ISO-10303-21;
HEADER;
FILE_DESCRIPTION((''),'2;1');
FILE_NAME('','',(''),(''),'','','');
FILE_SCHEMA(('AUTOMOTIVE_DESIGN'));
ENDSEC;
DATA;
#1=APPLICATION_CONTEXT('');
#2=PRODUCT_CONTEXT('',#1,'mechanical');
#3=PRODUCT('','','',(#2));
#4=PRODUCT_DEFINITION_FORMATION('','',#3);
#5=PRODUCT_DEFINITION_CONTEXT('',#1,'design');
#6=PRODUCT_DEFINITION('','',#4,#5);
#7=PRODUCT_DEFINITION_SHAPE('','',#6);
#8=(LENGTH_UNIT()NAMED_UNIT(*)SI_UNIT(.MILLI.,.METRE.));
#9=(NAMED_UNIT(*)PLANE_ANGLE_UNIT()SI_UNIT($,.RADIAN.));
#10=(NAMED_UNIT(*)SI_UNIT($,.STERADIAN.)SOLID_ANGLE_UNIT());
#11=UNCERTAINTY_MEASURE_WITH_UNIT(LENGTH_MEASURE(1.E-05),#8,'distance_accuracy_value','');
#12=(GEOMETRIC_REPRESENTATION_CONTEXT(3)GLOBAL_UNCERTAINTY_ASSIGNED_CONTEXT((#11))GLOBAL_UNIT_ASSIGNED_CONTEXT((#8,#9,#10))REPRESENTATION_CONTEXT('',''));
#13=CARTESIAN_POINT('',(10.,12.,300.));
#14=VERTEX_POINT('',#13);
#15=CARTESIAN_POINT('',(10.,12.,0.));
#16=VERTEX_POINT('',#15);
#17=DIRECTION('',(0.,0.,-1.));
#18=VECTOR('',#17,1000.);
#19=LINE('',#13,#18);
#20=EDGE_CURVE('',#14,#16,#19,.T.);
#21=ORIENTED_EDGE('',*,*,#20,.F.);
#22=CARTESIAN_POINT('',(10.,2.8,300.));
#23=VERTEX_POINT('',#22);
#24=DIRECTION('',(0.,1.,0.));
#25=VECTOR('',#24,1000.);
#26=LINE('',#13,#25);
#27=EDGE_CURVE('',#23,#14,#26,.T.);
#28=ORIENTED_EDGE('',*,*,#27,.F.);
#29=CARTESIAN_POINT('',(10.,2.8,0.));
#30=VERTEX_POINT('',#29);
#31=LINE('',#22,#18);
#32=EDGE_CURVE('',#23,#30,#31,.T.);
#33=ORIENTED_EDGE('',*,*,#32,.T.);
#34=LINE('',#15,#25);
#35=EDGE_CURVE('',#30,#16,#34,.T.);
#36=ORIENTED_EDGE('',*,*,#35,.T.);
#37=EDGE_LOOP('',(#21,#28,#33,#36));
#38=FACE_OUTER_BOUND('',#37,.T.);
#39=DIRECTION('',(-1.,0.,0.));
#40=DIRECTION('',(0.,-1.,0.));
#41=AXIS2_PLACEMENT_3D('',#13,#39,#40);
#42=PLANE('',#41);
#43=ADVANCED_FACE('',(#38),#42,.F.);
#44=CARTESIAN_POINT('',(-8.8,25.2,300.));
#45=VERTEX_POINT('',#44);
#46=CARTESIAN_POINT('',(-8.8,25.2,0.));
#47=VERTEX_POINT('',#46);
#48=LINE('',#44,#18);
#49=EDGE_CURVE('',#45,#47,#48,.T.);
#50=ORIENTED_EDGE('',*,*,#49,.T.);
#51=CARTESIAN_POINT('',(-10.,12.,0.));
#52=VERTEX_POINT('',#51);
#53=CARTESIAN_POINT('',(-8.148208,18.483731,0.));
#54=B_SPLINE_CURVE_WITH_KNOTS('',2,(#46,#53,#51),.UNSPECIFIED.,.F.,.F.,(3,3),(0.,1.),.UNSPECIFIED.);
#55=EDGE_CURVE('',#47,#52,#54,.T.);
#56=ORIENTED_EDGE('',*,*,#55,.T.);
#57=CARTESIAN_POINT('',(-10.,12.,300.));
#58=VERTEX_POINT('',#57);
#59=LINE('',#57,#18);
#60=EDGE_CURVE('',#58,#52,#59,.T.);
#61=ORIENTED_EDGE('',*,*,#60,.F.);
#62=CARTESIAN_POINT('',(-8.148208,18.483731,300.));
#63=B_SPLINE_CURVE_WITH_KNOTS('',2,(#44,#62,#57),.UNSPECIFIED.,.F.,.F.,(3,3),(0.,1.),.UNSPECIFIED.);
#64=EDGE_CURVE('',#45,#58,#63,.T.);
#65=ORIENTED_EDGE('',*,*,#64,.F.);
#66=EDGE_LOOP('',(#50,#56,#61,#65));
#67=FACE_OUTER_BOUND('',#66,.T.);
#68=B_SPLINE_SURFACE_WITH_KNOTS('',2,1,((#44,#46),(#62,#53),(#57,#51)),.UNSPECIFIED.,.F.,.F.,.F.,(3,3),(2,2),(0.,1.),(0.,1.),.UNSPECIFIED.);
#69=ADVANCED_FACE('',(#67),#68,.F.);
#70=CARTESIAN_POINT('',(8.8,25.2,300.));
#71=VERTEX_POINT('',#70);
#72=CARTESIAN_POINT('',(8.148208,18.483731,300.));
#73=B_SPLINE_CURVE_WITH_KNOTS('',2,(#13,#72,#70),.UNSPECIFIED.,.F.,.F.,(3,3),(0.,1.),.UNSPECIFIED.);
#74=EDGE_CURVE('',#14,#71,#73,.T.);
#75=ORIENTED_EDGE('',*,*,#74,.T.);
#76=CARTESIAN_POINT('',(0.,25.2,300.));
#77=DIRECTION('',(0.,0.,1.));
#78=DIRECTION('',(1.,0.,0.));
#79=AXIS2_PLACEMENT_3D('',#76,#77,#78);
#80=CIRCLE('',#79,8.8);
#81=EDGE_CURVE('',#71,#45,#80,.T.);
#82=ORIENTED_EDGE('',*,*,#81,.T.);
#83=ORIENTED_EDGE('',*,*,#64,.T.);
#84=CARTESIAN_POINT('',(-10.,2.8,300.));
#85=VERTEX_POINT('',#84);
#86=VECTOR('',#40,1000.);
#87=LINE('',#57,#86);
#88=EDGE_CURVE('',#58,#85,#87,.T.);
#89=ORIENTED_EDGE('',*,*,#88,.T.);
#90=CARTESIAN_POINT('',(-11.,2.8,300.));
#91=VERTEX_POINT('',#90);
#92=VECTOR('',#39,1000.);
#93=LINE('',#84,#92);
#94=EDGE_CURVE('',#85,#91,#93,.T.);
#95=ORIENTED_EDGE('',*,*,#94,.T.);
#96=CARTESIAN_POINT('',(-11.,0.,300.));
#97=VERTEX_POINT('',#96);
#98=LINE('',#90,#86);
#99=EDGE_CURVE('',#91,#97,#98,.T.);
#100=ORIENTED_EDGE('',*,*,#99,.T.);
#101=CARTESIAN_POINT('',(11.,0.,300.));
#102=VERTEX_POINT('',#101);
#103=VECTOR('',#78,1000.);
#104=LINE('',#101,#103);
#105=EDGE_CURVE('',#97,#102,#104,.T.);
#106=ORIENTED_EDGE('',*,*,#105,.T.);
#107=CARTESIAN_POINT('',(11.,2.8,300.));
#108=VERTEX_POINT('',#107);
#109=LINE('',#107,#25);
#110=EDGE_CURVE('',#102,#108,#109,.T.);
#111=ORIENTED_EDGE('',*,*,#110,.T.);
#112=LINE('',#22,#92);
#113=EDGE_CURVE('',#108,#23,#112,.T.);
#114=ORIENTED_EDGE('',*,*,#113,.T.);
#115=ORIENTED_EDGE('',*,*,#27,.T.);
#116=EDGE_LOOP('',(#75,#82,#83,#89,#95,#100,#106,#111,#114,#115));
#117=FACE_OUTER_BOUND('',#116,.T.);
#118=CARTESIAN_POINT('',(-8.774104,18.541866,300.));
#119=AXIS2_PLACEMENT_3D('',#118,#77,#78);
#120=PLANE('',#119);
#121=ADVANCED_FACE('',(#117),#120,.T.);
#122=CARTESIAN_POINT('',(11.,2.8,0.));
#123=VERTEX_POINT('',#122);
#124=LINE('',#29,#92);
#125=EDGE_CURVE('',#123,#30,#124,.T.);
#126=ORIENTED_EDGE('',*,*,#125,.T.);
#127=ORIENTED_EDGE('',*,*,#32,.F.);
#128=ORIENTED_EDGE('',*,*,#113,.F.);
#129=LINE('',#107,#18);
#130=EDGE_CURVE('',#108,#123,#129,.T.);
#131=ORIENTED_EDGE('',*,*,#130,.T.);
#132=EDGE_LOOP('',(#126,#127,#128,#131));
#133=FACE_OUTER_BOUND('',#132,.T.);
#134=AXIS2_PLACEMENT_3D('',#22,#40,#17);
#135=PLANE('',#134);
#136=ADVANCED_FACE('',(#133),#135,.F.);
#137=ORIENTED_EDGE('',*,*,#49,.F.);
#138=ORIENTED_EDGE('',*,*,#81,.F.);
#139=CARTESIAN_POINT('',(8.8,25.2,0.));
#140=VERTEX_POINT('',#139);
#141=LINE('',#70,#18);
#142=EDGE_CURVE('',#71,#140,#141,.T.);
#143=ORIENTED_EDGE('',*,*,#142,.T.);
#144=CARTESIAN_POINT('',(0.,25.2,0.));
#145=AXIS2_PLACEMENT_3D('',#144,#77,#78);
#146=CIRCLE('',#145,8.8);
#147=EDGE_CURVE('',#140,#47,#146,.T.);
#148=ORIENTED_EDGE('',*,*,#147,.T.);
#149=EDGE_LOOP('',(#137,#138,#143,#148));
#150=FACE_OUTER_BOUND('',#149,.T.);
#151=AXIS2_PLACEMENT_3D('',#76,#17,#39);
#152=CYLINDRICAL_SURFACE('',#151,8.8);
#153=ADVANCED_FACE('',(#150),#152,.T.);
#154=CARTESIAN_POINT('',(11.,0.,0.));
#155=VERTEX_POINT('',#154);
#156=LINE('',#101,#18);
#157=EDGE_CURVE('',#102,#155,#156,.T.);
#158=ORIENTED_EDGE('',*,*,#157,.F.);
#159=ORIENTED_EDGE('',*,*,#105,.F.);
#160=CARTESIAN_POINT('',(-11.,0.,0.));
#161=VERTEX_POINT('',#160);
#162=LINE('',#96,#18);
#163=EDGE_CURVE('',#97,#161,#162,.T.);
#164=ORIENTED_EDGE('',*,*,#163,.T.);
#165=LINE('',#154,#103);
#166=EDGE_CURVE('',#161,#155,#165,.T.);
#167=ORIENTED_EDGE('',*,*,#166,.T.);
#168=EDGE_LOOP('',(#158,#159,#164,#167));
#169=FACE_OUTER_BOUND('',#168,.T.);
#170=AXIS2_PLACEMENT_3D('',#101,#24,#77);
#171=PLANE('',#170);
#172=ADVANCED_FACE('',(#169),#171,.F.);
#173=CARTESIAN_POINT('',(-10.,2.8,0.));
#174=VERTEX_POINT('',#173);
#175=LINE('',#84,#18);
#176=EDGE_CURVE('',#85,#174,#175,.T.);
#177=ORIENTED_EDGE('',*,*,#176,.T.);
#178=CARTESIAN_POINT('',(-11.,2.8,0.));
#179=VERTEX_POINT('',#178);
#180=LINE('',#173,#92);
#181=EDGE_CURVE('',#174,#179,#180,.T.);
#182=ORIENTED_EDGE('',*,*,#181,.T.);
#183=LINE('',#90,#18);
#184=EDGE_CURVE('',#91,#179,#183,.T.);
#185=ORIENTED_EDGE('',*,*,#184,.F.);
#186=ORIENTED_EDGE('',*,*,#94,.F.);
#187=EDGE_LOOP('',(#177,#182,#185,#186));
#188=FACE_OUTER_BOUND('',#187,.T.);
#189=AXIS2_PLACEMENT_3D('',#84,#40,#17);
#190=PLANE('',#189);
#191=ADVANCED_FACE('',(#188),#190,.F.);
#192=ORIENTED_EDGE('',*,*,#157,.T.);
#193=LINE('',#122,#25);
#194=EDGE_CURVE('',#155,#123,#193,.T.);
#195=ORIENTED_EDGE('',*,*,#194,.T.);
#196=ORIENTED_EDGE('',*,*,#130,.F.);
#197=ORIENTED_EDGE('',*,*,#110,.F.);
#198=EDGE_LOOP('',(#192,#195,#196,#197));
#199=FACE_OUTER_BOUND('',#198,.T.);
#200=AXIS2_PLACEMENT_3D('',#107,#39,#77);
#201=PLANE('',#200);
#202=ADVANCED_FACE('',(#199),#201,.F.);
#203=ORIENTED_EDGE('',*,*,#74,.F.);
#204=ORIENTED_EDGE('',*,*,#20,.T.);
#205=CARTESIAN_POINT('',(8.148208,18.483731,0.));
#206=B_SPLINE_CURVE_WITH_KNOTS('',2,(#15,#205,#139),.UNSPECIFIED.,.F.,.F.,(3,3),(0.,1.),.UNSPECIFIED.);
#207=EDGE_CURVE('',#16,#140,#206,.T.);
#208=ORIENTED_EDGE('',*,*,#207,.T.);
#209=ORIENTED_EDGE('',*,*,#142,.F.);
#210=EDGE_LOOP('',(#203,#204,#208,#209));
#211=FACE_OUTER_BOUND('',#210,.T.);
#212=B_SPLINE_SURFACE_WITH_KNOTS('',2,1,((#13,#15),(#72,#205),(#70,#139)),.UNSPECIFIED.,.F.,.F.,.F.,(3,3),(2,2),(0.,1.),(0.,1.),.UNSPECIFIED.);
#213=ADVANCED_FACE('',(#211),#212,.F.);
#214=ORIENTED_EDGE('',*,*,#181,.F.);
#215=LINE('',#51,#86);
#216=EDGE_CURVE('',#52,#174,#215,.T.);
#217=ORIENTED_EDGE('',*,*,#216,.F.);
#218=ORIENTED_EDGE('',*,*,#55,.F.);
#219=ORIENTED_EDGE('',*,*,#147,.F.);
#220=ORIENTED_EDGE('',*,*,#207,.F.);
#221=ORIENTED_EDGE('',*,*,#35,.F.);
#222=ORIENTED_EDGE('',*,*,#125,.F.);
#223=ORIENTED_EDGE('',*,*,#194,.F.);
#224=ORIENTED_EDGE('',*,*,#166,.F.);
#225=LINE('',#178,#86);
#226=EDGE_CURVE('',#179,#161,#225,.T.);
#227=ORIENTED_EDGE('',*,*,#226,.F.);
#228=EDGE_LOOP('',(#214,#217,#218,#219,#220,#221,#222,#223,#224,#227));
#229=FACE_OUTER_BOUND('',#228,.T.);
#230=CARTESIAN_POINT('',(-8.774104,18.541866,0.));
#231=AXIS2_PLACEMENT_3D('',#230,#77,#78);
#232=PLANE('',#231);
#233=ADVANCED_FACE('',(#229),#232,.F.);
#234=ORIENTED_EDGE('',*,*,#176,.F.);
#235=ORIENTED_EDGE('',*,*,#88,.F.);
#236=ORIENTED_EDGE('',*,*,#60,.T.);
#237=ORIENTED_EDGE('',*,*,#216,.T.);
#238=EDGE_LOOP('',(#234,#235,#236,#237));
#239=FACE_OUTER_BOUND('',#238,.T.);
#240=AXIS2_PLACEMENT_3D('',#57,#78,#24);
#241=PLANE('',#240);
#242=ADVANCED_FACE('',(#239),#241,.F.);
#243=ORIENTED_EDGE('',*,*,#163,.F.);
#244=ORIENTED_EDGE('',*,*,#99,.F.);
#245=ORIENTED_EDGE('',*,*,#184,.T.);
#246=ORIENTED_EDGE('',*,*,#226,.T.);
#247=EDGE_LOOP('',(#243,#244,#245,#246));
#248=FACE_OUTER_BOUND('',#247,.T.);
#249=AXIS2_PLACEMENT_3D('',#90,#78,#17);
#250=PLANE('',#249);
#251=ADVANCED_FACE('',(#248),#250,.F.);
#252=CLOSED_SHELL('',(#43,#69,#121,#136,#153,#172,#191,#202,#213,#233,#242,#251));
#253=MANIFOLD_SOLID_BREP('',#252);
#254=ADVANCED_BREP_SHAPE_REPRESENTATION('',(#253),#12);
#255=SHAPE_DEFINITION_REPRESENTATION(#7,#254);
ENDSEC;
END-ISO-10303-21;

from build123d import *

# Parameters (mm, degrees)
EXTRUDE_1_DEPTH = 300


with BuildPart() as part:
    # 草图1 → 凸台-拉伸1 (new body)
    with BuildSketch(Plane.XY):
        with BuildLine():
            Line((10, 12), (10, 2.8))
            Line((10, 2.8), (11, 2.8))
            Line((11, 2.8), (11, 0))
            Line((11, 0), (-11, 0))
            Line((-11, 0), (-11, 2.8))
            Line((-11, 2.8), (-10, 2.8))
            Line((-10, 2.8), (-10, 12))
            add(Edge.make_bspline(
                [(-8.8, 25.2), (-8.148207528, 18.483731085), (-10, 12)],
                knots=[0, 0, 0, 1, 1, 1], degree=2))
            ThreePointArc((-8.8, 25.2), (0, 34), (8.8, 25.2))
            add(Edge.make_bspline(
                [(8.8, 25.2), (8.148207528, 18.483731085), (10, 12)],
                knots=[0, 0, 0, 1, 1, 1], degree=2))
        make_face()
    extrude(amount=EXTRUDE_1_DEPTH)


solid = part.part
